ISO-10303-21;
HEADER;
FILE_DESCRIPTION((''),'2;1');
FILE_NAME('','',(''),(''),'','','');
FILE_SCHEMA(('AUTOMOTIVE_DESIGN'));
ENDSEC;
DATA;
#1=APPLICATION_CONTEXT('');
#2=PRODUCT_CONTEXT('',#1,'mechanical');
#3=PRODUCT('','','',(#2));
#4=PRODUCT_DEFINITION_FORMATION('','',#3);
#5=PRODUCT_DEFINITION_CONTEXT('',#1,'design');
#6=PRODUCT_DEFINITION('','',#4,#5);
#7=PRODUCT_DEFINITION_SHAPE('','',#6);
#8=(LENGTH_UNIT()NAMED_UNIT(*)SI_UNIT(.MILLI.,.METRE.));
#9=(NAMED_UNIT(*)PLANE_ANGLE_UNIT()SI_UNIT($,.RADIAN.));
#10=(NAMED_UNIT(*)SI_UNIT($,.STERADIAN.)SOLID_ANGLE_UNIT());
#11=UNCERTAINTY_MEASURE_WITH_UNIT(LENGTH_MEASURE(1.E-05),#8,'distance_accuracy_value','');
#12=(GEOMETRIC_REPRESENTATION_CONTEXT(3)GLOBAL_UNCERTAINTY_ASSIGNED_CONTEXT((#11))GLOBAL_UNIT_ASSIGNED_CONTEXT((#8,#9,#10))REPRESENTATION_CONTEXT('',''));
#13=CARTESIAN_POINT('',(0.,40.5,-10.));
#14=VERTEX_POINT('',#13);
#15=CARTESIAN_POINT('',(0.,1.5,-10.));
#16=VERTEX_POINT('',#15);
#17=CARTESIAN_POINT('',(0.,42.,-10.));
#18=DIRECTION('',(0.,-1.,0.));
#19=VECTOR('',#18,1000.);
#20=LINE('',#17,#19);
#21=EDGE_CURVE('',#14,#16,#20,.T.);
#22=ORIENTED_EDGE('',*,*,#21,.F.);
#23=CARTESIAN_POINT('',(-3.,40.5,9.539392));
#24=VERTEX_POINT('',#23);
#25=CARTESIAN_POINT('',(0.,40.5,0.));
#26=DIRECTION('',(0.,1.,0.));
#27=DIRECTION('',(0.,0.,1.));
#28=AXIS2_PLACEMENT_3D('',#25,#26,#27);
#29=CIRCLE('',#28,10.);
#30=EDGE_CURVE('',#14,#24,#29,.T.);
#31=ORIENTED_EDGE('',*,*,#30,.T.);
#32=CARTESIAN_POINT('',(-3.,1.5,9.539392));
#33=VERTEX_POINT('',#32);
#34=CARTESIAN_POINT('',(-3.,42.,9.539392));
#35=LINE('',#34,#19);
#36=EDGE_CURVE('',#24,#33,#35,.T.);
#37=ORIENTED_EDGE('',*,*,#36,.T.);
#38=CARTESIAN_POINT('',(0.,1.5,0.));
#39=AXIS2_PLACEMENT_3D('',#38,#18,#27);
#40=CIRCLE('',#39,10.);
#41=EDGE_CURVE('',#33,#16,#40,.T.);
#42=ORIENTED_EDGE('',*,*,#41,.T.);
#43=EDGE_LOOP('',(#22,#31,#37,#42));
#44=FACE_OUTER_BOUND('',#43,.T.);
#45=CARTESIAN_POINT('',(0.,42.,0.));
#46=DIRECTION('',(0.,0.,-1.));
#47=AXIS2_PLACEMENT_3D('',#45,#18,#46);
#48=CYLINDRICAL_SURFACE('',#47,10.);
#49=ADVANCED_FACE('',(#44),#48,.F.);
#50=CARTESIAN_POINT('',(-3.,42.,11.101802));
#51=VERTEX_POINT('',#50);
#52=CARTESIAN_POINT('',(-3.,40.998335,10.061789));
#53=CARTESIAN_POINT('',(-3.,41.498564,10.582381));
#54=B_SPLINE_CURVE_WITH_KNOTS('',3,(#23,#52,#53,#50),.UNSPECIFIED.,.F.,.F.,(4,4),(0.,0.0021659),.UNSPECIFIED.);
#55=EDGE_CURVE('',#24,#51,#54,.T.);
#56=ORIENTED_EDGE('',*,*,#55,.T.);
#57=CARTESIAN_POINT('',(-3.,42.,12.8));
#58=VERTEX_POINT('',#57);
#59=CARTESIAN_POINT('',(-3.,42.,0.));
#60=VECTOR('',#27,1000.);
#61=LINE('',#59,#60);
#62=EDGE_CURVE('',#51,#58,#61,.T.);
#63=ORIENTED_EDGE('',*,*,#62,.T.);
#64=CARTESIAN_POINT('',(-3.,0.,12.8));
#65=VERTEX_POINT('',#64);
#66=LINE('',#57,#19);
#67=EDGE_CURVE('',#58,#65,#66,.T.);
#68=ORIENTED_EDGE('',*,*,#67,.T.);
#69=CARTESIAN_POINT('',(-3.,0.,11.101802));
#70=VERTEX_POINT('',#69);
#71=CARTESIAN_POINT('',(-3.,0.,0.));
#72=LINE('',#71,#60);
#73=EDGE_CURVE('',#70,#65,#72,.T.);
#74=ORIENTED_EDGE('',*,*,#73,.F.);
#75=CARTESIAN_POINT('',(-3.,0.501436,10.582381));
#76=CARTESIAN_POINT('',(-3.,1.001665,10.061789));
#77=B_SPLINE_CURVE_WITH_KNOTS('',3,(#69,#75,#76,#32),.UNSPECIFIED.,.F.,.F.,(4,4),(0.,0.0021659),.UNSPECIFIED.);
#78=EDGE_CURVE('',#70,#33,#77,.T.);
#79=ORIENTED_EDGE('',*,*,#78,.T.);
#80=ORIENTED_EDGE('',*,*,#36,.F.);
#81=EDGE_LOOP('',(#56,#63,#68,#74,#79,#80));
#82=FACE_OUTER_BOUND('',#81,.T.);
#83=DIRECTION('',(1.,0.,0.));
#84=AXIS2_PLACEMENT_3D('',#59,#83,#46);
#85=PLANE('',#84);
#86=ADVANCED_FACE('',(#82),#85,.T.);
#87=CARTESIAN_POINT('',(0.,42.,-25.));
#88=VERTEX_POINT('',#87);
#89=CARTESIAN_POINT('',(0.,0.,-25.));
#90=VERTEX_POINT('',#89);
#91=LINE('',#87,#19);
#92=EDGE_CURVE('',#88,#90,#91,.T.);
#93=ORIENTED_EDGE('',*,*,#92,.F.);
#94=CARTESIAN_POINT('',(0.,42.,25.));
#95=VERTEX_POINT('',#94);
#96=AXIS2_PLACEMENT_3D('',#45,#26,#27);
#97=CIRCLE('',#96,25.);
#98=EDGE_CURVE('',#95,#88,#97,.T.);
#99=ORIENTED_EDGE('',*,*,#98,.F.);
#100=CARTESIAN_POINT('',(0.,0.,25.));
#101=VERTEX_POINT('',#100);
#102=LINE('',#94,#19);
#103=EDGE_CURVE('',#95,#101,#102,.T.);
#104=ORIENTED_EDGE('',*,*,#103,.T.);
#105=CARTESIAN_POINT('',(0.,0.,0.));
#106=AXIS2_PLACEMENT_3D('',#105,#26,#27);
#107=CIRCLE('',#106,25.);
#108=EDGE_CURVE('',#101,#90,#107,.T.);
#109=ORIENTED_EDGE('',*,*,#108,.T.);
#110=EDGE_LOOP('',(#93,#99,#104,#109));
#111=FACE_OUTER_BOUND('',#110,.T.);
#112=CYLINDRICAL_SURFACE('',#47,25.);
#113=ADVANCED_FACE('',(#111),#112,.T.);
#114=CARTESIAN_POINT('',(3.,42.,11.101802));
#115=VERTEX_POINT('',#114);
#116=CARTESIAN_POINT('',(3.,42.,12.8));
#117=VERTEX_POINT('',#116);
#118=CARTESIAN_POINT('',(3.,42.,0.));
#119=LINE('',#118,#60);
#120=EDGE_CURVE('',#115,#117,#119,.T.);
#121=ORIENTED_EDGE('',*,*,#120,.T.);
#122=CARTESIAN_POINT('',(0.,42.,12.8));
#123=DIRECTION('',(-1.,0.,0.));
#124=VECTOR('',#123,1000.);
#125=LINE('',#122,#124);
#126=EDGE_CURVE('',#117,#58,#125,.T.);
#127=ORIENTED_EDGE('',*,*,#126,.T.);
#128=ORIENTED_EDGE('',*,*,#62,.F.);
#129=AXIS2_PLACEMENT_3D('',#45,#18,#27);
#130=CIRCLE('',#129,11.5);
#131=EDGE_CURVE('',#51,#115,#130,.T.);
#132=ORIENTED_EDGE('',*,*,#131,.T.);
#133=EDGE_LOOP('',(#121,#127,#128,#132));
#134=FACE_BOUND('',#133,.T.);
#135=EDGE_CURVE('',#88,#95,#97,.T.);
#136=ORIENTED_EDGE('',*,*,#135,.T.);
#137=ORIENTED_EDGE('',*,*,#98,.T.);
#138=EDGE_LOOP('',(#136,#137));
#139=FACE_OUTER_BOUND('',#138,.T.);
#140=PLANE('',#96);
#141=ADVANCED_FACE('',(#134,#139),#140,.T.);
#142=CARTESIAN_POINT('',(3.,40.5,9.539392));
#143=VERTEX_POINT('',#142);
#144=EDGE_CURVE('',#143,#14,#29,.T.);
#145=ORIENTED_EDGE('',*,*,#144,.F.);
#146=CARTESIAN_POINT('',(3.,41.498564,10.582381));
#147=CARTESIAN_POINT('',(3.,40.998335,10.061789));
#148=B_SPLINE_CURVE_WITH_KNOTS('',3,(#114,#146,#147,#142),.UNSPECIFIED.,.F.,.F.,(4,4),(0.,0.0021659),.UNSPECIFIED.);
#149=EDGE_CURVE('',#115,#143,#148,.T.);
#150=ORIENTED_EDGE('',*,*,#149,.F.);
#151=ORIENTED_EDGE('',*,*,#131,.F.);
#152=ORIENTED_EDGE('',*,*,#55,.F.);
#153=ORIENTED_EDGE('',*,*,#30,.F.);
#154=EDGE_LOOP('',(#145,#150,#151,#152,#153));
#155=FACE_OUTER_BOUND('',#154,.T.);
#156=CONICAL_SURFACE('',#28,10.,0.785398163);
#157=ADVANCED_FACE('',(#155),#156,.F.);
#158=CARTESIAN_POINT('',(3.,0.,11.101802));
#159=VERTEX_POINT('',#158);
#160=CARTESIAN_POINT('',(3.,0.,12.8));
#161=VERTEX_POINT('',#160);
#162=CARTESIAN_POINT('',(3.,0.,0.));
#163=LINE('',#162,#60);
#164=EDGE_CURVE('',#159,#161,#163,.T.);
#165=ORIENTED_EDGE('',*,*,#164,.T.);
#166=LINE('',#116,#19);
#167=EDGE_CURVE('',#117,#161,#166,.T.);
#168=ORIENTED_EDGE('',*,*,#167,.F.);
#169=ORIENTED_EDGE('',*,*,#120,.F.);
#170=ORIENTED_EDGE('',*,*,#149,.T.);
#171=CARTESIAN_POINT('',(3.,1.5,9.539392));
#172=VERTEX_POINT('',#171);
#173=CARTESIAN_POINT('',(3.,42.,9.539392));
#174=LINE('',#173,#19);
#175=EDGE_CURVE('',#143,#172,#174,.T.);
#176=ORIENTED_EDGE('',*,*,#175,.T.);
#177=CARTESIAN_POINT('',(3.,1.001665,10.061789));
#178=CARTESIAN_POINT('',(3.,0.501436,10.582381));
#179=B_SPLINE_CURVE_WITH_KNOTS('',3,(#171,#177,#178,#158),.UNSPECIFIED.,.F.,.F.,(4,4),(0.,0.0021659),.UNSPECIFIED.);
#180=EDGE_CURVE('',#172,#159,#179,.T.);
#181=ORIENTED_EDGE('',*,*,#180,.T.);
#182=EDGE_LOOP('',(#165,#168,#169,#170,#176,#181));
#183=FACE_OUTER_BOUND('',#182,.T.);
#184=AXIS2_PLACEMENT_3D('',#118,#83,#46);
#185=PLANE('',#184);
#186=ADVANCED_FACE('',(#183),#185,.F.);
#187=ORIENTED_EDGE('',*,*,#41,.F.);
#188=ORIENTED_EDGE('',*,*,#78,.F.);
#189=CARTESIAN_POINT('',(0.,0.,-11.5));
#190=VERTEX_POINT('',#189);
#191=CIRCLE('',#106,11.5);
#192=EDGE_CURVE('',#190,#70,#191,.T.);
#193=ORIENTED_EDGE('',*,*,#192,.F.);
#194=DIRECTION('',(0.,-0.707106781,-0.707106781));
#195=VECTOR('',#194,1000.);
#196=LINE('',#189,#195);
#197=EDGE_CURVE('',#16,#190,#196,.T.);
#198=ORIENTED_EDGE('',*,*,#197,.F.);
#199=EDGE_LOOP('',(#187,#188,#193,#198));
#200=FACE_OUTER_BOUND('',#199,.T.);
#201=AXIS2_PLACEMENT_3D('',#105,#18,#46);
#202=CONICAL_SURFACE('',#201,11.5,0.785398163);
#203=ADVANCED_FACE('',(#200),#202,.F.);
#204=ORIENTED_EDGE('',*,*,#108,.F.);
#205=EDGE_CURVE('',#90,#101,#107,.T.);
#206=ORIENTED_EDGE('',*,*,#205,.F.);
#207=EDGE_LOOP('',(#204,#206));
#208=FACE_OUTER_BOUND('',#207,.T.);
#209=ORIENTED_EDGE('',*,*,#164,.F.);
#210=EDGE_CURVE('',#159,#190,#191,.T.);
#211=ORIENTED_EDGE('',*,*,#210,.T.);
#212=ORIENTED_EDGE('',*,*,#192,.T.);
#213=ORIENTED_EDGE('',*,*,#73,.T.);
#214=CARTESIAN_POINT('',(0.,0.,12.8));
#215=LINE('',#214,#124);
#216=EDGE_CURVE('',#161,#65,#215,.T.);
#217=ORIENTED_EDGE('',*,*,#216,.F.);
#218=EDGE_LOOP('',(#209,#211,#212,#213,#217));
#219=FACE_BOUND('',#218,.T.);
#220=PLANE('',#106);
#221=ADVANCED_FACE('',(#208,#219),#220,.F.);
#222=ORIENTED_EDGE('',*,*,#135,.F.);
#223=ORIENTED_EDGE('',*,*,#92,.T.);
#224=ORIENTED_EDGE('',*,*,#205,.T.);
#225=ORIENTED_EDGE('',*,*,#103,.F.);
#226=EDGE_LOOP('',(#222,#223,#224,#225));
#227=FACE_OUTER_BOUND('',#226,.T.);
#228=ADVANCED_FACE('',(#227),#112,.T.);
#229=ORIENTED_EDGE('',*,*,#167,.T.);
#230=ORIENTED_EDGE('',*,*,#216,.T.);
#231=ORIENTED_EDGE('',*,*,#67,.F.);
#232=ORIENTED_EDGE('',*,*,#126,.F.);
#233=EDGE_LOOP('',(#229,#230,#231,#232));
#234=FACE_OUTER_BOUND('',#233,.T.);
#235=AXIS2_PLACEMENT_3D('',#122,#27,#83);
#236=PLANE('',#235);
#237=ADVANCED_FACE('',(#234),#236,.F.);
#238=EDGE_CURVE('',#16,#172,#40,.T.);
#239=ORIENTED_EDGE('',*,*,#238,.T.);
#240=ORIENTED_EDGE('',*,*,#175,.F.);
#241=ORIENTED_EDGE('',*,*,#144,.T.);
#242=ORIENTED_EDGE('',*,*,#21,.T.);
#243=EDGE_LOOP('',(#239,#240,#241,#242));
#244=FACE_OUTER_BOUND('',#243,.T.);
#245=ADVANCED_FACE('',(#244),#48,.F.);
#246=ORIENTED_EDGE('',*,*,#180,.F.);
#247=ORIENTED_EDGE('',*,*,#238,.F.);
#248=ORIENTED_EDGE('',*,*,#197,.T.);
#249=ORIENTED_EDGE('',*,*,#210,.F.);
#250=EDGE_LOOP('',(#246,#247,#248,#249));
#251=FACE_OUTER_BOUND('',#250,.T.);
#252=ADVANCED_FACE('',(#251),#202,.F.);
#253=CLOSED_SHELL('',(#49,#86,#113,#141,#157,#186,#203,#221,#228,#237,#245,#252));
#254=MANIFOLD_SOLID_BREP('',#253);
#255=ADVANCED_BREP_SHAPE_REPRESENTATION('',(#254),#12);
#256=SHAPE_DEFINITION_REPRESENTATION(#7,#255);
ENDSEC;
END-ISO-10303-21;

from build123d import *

# Parameters (mm, degrees)
SKETCH1_R           = 25
BOSS_EXTRUDE1_DEPTH = 42
CHAMFER1_SIZE       = 1.5


with BuildPart() as part:
    # Sketch1 → Boss-Extrude1 (new body)
    with BuildSketch(Plane(origin=(0, 0, 0), x_dir=(1, 0, 0), z_dir=(0, 1, 0))):
        with Locations(Location((0, 0, 0), (0, 0, 90))):
            Circle(SKETCH1_R)
        with BuildLine():
            ThreePointArc((10, 0), (8.062257748, -5.916079783), (3, -9.539392014))
            Line((3, -9.539392014), (3, -12.8))
            Line((3, -12.8), (-3, -12.8))
            Line((-3, -12.8), (-3, -9.539392014))
            ThreePointArc((-3, -9.539392014), (-5.916079783, 8.062257748), (10, 0))
        make_face(mode=Mode.SUBTRACT)
    extrude(amount=BOSS_EXTRUDE1_DEPTH)

    # Chamfer1
    chamfer1_edges = [part.edges().sort_by_distance(p)[0] for p in [
        (-5.916079783, 42, -8.062257748),
        (-5.916079783, 0, -8.062257748),
    ]]
    chamfer(chamfer1_edges, length=CHAMFER1_SIZE)


solid = part.part
